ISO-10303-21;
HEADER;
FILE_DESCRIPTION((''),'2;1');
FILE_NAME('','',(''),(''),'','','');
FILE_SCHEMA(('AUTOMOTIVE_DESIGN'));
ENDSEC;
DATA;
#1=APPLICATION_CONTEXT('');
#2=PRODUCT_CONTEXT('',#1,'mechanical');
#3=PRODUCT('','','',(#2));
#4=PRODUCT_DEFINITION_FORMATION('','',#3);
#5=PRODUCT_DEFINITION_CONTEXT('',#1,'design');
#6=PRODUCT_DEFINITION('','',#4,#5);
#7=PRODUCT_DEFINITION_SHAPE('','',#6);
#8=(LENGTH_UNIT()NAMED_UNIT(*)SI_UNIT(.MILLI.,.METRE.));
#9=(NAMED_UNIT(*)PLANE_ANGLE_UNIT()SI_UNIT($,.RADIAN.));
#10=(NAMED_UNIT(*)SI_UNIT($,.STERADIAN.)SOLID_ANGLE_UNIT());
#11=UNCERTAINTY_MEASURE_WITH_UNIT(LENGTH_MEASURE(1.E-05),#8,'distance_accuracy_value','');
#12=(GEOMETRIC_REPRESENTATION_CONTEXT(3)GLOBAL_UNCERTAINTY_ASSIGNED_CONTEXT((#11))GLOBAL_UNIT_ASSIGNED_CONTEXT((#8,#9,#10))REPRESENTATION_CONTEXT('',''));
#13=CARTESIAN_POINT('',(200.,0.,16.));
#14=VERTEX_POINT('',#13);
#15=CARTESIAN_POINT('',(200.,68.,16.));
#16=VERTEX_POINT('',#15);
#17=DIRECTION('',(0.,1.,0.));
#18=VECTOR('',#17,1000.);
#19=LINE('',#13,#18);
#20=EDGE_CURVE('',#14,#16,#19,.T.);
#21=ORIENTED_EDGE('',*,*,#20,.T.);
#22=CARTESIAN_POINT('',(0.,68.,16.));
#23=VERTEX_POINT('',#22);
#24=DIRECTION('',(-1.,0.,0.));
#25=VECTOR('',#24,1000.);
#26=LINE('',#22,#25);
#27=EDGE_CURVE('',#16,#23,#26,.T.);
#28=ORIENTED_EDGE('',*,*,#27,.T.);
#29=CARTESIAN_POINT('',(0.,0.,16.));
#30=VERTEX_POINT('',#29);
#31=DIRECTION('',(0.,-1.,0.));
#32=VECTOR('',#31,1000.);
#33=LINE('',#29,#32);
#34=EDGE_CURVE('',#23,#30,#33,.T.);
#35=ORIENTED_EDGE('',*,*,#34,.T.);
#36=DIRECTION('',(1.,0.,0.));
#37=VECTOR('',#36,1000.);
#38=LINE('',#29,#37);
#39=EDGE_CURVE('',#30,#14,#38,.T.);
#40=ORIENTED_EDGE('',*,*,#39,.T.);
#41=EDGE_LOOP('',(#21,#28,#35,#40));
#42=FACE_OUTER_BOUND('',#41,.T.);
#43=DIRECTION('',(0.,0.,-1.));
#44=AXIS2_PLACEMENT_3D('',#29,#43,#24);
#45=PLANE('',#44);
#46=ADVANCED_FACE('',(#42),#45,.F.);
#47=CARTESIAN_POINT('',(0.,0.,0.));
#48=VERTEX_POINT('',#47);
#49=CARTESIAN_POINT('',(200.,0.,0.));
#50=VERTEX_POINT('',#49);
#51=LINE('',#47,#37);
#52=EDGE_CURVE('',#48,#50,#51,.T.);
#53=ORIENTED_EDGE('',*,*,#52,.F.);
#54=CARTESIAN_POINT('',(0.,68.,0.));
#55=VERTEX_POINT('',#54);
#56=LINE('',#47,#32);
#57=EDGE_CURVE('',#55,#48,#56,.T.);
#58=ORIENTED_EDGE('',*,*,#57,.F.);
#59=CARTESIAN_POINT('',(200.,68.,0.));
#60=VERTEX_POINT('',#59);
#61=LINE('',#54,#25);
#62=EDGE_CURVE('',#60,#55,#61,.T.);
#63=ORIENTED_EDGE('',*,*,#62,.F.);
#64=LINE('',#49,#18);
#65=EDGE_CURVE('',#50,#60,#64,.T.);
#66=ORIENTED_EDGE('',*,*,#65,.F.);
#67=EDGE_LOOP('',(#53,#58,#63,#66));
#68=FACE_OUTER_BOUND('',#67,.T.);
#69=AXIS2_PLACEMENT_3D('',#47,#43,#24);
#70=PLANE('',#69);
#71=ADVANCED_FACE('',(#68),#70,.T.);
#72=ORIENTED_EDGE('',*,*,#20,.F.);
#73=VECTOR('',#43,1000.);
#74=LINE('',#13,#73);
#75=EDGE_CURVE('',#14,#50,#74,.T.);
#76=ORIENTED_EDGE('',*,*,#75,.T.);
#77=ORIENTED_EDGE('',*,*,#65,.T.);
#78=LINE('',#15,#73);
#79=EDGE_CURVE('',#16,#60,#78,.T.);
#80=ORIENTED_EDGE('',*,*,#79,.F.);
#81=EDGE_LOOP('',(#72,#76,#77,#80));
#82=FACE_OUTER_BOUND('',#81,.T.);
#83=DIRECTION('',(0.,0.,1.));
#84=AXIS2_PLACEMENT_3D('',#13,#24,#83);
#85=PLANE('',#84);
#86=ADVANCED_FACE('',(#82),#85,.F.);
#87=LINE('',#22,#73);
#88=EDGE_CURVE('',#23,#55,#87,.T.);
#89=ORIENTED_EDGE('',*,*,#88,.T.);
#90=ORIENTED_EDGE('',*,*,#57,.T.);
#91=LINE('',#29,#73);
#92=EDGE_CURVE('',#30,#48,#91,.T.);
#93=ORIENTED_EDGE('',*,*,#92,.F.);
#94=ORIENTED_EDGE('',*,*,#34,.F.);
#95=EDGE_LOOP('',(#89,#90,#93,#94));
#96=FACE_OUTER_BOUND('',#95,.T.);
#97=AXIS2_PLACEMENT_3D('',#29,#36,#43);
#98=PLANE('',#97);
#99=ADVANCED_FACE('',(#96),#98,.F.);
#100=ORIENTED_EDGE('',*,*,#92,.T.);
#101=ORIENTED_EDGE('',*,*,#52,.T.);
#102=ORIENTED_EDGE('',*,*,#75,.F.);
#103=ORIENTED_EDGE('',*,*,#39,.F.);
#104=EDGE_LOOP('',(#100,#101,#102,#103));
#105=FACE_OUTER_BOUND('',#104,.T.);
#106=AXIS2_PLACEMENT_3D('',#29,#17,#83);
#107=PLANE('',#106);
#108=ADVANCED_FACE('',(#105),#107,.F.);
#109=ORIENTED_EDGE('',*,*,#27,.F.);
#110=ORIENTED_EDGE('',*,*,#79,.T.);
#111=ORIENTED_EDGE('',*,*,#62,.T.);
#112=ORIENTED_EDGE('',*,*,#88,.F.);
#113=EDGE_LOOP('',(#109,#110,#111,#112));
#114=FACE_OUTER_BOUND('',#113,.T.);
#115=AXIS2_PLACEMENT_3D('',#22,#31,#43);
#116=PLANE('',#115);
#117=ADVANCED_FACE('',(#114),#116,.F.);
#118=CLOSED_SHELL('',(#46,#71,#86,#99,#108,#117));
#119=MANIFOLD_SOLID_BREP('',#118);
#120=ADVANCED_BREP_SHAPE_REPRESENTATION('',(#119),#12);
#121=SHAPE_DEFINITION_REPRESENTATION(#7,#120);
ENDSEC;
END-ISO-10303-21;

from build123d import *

# Parameters (mm, degrees)
SKETCH1_W           = 200
SKETCH1_H           = 68
BOSS_EXTRUDE1_DEPTH = 16


with BuildPart() as part:
    # Sketch1 → Boss-Extrude1 (new body)
    with BuildSketch(Plane.XY):
        with Locations((100, 34)):
            Rectangle(SKETCH1_W, SKETCH1_H)
    extrude(amount=BOSS_EXTRUDE1_DEPTH)


solid = part.part
